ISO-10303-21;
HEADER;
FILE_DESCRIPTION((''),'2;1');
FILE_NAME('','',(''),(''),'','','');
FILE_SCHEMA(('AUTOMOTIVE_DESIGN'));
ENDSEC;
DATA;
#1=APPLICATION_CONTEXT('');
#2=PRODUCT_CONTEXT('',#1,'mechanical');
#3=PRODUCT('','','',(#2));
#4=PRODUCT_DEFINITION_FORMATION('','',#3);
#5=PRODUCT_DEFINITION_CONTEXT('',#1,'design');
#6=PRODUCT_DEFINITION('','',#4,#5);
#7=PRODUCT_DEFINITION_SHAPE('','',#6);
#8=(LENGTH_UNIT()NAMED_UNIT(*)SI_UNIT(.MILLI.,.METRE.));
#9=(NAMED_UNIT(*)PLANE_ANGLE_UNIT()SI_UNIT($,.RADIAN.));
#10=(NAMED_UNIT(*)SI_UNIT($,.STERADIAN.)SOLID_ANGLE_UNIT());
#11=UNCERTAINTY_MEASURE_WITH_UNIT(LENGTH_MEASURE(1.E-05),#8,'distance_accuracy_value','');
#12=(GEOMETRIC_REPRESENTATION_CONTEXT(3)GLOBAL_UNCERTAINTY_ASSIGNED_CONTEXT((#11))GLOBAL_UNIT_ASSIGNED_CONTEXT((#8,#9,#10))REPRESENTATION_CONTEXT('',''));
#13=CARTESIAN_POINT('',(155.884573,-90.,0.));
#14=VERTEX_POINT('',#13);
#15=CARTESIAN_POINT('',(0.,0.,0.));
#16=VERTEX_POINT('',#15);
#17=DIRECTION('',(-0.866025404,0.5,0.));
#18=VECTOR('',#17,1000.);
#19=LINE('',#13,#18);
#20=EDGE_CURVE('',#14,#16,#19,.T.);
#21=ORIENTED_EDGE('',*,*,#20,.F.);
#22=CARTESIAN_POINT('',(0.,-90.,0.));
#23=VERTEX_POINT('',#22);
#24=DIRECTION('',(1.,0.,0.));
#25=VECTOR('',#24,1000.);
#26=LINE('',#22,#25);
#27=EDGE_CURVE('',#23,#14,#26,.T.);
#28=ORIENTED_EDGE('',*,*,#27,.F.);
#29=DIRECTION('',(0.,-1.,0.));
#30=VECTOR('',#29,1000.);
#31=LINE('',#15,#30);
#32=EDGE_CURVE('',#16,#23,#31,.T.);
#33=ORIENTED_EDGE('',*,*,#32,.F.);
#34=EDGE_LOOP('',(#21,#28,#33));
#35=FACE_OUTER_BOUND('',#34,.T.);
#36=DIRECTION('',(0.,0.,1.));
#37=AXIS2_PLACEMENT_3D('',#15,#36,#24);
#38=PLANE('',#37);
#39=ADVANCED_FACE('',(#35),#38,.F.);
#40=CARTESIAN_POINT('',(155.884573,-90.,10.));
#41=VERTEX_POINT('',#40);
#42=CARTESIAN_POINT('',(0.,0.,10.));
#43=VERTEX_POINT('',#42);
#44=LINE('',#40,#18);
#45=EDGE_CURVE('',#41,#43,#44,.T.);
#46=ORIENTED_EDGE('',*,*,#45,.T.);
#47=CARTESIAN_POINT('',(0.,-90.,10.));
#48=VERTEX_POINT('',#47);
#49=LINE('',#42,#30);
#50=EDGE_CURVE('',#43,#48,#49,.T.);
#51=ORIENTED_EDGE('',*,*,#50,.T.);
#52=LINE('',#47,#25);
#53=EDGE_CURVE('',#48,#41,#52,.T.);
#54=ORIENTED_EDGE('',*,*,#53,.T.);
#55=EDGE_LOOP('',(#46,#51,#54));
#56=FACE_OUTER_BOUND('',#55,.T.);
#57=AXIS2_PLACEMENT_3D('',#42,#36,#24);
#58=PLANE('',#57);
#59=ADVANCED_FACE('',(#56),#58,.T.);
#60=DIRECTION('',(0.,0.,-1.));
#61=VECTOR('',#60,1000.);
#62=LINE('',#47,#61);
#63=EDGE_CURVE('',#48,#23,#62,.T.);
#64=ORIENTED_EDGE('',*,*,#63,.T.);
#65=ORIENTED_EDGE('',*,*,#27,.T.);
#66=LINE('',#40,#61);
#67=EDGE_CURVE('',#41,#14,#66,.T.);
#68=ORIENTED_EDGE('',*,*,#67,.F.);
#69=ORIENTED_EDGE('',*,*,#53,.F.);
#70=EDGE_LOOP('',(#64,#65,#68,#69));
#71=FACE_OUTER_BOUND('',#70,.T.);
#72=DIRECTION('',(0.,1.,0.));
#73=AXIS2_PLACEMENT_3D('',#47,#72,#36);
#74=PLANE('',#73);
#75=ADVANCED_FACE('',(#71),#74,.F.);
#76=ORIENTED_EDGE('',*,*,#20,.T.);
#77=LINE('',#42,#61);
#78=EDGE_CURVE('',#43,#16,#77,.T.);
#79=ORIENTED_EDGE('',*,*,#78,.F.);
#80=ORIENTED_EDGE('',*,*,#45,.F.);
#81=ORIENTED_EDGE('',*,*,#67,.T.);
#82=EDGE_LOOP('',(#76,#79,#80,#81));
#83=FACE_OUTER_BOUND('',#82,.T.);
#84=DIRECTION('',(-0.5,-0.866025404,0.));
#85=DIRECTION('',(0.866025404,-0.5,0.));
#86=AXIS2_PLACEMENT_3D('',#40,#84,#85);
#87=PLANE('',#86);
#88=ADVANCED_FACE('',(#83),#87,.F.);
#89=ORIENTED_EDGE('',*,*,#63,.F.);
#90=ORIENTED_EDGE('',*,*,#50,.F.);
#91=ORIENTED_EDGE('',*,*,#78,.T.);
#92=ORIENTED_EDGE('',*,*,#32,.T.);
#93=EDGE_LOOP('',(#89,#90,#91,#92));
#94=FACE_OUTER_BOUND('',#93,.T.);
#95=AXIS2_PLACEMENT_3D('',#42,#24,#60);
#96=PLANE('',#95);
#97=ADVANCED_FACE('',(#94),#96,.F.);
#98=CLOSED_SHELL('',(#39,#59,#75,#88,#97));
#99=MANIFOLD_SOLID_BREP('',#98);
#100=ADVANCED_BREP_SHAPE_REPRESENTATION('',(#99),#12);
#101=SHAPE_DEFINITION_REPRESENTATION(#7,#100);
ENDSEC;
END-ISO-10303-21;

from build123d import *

# Parameters (mm, degrees)
BOSS_EXTRUDE1_DEPTH = 10


with BuildPart() as part:
    # Sketch1 → Boss-Extrude1 (new body)
    with BuildSketch(Plane.XY):
        Polygon((0, 0), (0, -90), (155.884572681, -90), align=None)
    extrude(amount=BOSS_EXTRUDE1_DEPTH)


solid = part.part
